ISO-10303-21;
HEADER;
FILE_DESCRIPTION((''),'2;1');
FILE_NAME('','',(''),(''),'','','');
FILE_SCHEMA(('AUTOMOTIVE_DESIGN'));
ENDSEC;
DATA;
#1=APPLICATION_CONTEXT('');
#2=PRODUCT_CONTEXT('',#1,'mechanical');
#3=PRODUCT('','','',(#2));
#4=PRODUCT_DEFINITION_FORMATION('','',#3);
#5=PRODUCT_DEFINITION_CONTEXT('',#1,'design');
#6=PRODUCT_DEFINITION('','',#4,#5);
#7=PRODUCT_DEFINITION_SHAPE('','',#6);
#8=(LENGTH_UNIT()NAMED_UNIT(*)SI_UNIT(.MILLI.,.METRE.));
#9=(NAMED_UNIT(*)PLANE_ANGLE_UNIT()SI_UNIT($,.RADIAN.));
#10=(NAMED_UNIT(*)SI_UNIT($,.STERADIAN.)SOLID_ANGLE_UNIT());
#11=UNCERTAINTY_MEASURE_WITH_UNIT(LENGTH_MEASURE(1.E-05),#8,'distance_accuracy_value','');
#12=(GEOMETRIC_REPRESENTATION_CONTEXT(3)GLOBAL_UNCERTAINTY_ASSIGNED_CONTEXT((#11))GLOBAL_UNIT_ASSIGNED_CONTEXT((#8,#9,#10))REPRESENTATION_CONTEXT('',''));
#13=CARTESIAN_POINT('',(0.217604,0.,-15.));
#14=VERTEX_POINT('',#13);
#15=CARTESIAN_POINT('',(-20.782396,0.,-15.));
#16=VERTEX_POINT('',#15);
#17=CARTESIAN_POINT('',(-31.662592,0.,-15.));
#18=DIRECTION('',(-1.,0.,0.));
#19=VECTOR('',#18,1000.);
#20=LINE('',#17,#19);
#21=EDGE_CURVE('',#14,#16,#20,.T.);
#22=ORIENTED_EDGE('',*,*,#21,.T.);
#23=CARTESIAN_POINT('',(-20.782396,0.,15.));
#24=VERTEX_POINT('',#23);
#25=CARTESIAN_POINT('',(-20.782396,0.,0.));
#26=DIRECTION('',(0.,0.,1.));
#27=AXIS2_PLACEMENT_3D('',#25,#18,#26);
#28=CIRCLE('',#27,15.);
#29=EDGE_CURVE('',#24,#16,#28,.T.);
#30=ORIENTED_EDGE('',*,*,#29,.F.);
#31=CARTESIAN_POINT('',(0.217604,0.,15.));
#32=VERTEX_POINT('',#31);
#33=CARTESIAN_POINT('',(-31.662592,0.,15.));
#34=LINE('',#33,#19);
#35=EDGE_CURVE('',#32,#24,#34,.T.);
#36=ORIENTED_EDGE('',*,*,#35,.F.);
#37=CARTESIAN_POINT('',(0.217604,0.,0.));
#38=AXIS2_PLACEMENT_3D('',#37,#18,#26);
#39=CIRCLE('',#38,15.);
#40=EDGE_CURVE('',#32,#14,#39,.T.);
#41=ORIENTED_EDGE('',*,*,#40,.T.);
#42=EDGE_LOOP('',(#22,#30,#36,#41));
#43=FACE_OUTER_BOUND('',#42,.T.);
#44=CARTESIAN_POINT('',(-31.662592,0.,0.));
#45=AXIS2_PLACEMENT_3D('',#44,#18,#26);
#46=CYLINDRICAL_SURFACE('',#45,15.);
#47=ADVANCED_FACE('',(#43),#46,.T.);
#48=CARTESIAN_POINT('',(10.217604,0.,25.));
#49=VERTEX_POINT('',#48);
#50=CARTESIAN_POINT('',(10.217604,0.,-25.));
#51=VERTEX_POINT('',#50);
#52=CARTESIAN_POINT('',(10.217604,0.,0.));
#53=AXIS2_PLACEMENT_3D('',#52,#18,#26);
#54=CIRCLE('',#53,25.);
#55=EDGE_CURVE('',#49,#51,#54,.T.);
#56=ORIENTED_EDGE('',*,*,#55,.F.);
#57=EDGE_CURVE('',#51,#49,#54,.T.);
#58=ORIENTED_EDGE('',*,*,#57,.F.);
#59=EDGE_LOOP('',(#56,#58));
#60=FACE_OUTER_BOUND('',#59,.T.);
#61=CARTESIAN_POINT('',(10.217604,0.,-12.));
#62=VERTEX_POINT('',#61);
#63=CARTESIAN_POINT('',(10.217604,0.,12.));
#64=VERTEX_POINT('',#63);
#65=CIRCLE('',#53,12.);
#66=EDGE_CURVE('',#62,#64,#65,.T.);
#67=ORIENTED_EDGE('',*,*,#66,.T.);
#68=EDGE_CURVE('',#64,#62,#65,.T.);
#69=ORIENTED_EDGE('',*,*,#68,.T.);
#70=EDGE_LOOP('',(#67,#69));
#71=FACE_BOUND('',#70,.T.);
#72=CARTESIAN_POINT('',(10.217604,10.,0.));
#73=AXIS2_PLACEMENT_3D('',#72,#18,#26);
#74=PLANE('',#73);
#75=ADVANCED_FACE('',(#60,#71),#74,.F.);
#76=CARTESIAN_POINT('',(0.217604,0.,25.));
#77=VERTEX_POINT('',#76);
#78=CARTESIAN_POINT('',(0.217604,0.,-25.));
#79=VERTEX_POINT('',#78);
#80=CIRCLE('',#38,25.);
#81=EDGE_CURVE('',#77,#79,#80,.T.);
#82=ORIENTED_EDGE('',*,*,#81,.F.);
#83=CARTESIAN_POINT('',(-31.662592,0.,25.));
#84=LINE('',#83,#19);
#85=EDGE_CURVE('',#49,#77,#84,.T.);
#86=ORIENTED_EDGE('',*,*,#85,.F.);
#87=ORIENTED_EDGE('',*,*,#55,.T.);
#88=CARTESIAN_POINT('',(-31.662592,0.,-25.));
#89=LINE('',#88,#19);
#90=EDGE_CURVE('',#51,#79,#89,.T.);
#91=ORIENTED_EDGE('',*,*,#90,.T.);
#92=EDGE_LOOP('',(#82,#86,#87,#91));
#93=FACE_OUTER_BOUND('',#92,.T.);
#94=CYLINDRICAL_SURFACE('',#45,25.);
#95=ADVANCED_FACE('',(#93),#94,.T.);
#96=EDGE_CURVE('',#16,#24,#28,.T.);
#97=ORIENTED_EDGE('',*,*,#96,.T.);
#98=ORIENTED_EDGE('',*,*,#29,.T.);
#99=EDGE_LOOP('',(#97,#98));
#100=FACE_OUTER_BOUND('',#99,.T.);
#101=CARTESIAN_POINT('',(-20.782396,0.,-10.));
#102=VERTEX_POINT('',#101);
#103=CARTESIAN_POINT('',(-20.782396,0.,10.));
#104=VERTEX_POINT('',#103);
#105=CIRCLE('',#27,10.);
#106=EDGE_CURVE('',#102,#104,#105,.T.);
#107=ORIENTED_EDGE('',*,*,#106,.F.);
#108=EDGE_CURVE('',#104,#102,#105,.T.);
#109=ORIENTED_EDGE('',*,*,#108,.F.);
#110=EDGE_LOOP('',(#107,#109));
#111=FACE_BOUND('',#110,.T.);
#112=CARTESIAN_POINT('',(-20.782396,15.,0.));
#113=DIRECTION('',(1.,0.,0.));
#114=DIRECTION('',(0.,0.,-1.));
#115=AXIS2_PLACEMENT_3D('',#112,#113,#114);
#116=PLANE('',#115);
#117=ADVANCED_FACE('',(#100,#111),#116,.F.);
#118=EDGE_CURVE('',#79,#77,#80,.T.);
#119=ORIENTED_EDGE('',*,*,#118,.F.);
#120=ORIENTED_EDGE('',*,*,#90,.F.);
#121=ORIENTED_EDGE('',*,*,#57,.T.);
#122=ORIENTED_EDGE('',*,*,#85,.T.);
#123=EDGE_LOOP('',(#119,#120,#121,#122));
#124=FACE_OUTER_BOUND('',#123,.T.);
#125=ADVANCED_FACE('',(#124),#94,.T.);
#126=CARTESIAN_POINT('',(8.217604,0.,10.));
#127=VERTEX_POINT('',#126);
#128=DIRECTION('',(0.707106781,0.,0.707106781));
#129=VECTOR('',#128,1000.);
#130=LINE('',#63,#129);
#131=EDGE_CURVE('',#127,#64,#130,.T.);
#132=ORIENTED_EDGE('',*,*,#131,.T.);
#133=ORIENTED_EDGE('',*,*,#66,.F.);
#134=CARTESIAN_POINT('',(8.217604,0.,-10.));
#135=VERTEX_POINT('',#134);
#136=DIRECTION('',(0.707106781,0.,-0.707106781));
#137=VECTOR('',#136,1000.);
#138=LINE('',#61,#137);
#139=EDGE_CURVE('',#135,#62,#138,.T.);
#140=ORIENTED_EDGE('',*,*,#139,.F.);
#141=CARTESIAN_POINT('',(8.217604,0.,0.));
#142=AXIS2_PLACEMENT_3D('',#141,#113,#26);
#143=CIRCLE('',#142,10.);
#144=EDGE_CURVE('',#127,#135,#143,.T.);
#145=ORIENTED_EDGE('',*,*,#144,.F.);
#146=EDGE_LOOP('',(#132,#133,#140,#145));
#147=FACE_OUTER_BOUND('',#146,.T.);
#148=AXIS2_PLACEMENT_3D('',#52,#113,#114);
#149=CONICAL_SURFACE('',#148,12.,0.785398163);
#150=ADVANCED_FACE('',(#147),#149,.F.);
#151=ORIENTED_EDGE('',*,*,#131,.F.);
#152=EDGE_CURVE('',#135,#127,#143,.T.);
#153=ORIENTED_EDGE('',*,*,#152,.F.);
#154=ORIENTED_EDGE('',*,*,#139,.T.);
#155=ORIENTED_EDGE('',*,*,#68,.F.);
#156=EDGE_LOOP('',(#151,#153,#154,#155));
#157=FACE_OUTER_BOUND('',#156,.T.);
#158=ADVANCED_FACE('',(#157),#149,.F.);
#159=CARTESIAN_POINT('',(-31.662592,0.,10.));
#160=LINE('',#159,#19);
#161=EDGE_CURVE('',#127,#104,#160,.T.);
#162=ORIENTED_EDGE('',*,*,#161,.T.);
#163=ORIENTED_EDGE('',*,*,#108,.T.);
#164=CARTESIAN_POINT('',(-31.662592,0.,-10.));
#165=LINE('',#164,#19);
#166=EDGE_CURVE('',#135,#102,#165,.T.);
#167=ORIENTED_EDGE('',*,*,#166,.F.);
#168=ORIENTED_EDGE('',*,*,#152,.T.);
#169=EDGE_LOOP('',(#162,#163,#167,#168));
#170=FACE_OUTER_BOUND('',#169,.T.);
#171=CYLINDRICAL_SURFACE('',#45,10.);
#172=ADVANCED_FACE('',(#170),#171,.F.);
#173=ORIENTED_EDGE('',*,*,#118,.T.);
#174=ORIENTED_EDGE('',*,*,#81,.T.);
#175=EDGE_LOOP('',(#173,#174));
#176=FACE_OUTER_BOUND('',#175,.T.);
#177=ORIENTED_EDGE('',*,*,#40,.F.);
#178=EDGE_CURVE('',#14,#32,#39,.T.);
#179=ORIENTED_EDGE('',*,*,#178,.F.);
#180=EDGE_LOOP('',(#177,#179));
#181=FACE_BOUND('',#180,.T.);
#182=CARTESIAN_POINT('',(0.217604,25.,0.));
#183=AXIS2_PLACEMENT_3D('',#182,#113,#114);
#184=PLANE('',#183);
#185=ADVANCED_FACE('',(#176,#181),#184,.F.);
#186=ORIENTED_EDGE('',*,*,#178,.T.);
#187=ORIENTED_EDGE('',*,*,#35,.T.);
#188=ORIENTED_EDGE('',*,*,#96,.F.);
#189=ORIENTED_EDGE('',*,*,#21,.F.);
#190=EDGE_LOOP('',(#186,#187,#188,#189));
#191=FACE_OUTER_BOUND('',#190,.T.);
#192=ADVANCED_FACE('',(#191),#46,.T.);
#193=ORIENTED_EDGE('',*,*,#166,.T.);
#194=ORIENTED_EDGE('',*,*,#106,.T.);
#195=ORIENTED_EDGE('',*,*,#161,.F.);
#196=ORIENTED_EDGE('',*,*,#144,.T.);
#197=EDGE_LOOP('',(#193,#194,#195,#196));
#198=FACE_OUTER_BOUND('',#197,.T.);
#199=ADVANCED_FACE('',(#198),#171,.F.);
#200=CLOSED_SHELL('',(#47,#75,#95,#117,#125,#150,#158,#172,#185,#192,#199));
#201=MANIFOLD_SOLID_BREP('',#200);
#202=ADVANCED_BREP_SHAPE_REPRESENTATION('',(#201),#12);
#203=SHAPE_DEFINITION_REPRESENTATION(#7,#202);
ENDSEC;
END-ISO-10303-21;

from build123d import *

# Parameters (mm, degrees)
CHAMFER1_SIZE = 2


with BuildPart() as part:
    # Sketch1 → Revolve1 (revolve)
    with BuildSketch(Plane.XY, mode=Mode.PRIVATE) as revolve1_sk:
        Polygon((-20.782396088, 10), (10.217603912, 10), (10.217603912, 25), (0.217603912, 25), (0.217603912, 15), (-20.782396088, 15), align=None)
    revolve(revolve1_sk.sketch.rotate(Axis((-31.662591687, 0, 0), (1, 0, 0)), 90), axis=Axis((-31.662591687, 0, 0), (1, 0, 0)))

    # Chamfer1
    chamfer1_edges = [part.edges().sort_by_distance(p)[0] for p in [
        (10.217603912, 0, -10),
    ]]
    chamfer(chamfer1_edges, length=CHAMFER1_SIZE)


solid = part.part
